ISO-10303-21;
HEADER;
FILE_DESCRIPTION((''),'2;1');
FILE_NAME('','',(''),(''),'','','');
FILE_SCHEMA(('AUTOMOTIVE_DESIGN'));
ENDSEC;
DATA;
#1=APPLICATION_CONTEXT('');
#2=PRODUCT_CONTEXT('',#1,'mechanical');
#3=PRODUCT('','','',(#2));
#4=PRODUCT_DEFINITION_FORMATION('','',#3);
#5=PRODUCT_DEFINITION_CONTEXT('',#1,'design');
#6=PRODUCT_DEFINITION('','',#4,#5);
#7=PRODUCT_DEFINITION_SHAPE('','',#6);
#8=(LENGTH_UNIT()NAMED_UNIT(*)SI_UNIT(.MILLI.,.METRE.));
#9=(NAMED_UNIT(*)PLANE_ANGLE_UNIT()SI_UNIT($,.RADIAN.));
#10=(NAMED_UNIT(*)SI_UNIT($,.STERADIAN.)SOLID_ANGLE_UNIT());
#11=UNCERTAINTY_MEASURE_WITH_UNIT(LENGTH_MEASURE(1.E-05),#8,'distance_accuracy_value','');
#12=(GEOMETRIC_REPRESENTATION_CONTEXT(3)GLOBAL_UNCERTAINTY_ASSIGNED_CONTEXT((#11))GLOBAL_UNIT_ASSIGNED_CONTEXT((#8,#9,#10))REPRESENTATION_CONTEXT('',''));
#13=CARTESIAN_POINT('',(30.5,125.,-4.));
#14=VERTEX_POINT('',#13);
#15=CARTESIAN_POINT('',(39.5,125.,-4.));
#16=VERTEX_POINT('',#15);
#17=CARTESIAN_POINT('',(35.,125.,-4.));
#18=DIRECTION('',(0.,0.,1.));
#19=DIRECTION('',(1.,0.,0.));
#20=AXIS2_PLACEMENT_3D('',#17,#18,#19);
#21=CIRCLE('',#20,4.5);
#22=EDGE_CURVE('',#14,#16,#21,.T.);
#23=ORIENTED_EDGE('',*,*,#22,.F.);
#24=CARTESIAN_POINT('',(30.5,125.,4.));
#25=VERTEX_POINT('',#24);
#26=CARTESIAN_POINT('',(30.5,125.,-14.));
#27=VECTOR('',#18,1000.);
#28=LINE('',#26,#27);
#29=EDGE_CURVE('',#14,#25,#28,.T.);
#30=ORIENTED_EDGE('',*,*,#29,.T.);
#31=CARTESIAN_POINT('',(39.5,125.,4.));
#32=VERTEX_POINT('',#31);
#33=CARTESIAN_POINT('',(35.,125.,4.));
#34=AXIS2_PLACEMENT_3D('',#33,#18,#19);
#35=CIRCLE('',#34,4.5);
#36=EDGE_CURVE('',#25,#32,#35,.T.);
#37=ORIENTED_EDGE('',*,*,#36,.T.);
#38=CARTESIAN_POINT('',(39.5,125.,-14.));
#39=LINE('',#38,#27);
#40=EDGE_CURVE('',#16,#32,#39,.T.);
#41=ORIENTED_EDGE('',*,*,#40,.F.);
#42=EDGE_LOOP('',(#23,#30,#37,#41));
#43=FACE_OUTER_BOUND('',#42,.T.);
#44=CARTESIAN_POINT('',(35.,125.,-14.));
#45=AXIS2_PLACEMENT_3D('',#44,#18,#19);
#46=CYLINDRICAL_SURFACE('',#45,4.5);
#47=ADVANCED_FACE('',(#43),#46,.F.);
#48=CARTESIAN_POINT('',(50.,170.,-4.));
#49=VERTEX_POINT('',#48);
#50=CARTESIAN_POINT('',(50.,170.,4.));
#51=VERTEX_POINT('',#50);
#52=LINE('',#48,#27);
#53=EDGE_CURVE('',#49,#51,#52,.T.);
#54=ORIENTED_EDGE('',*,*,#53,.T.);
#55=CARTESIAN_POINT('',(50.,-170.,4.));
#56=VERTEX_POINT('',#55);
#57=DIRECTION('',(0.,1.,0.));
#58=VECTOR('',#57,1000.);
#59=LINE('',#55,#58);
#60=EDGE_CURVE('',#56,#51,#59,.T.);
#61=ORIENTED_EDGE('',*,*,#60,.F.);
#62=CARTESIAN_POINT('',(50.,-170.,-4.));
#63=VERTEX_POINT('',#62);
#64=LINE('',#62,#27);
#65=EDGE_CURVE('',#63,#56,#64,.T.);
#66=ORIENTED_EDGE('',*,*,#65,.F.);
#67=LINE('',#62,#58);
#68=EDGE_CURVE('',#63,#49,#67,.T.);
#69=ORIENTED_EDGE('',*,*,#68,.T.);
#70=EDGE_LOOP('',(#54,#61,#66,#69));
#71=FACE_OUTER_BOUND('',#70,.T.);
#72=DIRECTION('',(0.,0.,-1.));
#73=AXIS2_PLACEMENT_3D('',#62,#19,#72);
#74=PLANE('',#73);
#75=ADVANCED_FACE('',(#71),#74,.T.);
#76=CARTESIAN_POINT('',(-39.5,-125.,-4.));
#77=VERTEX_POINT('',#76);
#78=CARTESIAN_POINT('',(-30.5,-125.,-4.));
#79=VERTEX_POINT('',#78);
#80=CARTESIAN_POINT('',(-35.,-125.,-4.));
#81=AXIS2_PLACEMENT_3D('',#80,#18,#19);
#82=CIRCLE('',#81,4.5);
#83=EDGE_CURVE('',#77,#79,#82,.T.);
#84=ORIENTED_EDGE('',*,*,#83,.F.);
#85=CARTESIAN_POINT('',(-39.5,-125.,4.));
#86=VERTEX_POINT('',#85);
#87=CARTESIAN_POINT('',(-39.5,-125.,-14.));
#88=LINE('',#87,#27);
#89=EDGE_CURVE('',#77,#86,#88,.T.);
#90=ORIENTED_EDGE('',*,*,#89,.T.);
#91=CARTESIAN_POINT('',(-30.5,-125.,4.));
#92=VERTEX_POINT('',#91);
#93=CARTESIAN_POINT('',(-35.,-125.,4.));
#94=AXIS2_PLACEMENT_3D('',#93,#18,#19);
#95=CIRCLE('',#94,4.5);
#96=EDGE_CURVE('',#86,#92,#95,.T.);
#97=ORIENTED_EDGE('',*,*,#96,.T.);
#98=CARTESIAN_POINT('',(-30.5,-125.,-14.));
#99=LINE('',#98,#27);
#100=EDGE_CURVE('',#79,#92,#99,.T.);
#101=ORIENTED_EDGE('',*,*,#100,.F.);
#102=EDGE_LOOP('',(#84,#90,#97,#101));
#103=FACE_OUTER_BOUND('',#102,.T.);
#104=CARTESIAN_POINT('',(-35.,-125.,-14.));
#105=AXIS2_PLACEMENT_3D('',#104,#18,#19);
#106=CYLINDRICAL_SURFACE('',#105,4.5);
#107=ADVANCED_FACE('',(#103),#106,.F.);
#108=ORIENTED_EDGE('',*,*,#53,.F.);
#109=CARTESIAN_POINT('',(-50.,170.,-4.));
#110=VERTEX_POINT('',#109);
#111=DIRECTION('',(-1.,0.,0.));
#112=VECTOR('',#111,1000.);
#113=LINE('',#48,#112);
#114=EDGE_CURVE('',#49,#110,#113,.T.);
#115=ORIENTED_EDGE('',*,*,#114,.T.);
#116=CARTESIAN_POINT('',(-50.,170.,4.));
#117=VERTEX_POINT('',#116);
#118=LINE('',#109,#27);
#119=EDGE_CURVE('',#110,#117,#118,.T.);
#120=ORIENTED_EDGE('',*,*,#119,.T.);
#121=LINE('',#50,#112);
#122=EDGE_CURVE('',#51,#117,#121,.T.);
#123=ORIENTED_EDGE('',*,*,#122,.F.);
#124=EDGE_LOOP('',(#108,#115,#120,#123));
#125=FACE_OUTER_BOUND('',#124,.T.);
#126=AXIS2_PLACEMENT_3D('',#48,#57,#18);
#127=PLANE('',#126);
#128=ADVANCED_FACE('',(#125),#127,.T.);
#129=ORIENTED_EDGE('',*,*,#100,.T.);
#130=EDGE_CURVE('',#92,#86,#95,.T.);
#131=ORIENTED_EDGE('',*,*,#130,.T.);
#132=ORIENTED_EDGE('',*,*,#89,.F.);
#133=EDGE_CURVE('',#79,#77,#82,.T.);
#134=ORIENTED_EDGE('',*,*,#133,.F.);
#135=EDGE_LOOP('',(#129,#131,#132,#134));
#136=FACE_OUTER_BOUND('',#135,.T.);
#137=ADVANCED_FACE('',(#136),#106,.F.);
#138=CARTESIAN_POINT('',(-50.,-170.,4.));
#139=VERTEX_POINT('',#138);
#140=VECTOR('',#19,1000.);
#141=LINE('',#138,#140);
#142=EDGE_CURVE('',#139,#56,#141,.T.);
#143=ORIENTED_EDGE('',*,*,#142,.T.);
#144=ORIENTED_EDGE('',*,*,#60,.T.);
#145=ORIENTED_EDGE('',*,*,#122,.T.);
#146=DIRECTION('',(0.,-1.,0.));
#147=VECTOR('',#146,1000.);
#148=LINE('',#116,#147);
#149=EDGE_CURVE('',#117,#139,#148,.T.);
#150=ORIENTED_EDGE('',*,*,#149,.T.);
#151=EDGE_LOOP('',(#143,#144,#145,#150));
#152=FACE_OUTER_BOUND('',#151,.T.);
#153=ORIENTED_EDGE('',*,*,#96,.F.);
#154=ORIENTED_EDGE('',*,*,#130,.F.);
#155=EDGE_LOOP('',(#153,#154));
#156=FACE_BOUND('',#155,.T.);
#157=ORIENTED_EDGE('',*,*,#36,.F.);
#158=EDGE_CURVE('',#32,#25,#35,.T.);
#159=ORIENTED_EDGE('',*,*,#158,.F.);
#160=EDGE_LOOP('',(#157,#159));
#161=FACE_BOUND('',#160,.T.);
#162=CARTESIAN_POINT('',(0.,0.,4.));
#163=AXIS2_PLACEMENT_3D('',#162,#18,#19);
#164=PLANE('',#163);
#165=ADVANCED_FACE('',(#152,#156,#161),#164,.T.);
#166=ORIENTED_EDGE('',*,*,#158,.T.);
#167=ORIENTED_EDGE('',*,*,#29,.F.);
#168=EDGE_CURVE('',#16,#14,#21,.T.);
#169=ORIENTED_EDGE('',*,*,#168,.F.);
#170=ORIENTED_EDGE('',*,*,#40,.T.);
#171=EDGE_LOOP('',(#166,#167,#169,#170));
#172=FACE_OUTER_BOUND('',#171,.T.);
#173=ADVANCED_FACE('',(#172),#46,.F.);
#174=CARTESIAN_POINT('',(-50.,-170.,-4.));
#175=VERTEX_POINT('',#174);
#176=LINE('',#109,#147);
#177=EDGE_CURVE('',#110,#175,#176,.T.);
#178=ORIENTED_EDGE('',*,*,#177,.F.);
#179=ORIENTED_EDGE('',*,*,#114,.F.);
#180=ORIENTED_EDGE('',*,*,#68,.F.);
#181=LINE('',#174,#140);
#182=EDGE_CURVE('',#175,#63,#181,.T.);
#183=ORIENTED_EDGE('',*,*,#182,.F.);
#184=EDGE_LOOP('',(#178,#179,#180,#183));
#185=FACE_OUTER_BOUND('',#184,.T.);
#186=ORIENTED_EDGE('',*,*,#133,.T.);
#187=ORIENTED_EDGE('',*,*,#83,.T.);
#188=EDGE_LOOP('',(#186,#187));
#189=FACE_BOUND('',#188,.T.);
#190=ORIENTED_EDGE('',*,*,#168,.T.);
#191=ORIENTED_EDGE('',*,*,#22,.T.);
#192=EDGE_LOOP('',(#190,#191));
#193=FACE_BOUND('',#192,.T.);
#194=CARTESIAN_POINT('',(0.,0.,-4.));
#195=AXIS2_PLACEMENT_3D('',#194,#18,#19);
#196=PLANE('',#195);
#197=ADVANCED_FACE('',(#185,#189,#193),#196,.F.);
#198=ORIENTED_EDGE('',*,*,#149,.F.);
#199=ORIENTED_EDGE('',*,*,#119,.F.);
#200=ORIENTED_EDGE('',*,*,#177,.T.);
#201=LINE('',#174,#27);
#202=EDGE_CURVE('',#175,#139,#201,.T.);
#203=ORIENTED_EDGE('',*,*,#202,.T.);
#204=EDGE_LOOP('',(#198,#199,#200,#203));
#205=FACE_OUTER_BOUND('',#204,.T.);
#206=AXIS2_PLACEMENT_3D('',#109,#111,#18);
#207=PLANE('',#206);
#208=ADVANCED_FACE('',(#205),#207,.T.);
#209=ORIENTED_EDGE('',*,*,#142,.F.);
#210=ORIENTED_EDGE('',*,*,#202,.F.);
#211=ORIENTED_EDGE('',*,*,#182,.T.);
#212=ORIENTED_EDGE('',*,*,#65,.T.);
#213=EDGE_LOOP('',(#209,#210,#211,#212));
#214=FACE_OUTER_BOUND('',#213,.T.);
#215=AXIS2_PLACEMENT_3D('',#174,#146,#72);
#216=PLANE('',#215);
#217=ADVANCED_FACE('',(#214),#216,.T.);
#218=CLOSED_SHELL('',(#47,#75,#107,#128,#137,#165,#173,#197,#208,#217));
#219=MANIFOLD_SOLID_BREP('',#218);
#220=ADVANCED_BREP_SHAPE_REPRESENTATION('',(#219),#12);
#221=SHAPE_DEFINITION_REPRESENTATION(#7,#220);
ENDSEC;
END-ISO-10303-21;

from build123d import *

# Parameters (mm, degrees)
SKETCH_1_W          = 100
SKETCH_1_H          = 340
EXTRUDE_1_DEPTH     = 4
SKETCH_2_R          = 4.5
CUT_EXTRUDE_1_DEPTH = 14


with BuildPart() as part:
    # 草图1 → 凸台-拉伸1 (new, symmetric)
    with BuildSketch(Plane.XY):
        Rectangle(SKETCH_1_W, SKETCH_1_H)
    extrude(amount=EXTRUDE_1_DEPTH, both=True)

    # 草图2 → 切除-拉伸1 (cut, symmetric)
    with BuildSketch(Plane.XY):
        with Locations((-35, -125)):
            Circle(SKETCH_2_R)
        with Locations((35, 125)):
            Circle(SKETCH_2_R)
    extrude(amount=CUT_EXTRUDE_1_DEPTH, both=True, mode=Mode.SUBTRACT)


solid = part.part
